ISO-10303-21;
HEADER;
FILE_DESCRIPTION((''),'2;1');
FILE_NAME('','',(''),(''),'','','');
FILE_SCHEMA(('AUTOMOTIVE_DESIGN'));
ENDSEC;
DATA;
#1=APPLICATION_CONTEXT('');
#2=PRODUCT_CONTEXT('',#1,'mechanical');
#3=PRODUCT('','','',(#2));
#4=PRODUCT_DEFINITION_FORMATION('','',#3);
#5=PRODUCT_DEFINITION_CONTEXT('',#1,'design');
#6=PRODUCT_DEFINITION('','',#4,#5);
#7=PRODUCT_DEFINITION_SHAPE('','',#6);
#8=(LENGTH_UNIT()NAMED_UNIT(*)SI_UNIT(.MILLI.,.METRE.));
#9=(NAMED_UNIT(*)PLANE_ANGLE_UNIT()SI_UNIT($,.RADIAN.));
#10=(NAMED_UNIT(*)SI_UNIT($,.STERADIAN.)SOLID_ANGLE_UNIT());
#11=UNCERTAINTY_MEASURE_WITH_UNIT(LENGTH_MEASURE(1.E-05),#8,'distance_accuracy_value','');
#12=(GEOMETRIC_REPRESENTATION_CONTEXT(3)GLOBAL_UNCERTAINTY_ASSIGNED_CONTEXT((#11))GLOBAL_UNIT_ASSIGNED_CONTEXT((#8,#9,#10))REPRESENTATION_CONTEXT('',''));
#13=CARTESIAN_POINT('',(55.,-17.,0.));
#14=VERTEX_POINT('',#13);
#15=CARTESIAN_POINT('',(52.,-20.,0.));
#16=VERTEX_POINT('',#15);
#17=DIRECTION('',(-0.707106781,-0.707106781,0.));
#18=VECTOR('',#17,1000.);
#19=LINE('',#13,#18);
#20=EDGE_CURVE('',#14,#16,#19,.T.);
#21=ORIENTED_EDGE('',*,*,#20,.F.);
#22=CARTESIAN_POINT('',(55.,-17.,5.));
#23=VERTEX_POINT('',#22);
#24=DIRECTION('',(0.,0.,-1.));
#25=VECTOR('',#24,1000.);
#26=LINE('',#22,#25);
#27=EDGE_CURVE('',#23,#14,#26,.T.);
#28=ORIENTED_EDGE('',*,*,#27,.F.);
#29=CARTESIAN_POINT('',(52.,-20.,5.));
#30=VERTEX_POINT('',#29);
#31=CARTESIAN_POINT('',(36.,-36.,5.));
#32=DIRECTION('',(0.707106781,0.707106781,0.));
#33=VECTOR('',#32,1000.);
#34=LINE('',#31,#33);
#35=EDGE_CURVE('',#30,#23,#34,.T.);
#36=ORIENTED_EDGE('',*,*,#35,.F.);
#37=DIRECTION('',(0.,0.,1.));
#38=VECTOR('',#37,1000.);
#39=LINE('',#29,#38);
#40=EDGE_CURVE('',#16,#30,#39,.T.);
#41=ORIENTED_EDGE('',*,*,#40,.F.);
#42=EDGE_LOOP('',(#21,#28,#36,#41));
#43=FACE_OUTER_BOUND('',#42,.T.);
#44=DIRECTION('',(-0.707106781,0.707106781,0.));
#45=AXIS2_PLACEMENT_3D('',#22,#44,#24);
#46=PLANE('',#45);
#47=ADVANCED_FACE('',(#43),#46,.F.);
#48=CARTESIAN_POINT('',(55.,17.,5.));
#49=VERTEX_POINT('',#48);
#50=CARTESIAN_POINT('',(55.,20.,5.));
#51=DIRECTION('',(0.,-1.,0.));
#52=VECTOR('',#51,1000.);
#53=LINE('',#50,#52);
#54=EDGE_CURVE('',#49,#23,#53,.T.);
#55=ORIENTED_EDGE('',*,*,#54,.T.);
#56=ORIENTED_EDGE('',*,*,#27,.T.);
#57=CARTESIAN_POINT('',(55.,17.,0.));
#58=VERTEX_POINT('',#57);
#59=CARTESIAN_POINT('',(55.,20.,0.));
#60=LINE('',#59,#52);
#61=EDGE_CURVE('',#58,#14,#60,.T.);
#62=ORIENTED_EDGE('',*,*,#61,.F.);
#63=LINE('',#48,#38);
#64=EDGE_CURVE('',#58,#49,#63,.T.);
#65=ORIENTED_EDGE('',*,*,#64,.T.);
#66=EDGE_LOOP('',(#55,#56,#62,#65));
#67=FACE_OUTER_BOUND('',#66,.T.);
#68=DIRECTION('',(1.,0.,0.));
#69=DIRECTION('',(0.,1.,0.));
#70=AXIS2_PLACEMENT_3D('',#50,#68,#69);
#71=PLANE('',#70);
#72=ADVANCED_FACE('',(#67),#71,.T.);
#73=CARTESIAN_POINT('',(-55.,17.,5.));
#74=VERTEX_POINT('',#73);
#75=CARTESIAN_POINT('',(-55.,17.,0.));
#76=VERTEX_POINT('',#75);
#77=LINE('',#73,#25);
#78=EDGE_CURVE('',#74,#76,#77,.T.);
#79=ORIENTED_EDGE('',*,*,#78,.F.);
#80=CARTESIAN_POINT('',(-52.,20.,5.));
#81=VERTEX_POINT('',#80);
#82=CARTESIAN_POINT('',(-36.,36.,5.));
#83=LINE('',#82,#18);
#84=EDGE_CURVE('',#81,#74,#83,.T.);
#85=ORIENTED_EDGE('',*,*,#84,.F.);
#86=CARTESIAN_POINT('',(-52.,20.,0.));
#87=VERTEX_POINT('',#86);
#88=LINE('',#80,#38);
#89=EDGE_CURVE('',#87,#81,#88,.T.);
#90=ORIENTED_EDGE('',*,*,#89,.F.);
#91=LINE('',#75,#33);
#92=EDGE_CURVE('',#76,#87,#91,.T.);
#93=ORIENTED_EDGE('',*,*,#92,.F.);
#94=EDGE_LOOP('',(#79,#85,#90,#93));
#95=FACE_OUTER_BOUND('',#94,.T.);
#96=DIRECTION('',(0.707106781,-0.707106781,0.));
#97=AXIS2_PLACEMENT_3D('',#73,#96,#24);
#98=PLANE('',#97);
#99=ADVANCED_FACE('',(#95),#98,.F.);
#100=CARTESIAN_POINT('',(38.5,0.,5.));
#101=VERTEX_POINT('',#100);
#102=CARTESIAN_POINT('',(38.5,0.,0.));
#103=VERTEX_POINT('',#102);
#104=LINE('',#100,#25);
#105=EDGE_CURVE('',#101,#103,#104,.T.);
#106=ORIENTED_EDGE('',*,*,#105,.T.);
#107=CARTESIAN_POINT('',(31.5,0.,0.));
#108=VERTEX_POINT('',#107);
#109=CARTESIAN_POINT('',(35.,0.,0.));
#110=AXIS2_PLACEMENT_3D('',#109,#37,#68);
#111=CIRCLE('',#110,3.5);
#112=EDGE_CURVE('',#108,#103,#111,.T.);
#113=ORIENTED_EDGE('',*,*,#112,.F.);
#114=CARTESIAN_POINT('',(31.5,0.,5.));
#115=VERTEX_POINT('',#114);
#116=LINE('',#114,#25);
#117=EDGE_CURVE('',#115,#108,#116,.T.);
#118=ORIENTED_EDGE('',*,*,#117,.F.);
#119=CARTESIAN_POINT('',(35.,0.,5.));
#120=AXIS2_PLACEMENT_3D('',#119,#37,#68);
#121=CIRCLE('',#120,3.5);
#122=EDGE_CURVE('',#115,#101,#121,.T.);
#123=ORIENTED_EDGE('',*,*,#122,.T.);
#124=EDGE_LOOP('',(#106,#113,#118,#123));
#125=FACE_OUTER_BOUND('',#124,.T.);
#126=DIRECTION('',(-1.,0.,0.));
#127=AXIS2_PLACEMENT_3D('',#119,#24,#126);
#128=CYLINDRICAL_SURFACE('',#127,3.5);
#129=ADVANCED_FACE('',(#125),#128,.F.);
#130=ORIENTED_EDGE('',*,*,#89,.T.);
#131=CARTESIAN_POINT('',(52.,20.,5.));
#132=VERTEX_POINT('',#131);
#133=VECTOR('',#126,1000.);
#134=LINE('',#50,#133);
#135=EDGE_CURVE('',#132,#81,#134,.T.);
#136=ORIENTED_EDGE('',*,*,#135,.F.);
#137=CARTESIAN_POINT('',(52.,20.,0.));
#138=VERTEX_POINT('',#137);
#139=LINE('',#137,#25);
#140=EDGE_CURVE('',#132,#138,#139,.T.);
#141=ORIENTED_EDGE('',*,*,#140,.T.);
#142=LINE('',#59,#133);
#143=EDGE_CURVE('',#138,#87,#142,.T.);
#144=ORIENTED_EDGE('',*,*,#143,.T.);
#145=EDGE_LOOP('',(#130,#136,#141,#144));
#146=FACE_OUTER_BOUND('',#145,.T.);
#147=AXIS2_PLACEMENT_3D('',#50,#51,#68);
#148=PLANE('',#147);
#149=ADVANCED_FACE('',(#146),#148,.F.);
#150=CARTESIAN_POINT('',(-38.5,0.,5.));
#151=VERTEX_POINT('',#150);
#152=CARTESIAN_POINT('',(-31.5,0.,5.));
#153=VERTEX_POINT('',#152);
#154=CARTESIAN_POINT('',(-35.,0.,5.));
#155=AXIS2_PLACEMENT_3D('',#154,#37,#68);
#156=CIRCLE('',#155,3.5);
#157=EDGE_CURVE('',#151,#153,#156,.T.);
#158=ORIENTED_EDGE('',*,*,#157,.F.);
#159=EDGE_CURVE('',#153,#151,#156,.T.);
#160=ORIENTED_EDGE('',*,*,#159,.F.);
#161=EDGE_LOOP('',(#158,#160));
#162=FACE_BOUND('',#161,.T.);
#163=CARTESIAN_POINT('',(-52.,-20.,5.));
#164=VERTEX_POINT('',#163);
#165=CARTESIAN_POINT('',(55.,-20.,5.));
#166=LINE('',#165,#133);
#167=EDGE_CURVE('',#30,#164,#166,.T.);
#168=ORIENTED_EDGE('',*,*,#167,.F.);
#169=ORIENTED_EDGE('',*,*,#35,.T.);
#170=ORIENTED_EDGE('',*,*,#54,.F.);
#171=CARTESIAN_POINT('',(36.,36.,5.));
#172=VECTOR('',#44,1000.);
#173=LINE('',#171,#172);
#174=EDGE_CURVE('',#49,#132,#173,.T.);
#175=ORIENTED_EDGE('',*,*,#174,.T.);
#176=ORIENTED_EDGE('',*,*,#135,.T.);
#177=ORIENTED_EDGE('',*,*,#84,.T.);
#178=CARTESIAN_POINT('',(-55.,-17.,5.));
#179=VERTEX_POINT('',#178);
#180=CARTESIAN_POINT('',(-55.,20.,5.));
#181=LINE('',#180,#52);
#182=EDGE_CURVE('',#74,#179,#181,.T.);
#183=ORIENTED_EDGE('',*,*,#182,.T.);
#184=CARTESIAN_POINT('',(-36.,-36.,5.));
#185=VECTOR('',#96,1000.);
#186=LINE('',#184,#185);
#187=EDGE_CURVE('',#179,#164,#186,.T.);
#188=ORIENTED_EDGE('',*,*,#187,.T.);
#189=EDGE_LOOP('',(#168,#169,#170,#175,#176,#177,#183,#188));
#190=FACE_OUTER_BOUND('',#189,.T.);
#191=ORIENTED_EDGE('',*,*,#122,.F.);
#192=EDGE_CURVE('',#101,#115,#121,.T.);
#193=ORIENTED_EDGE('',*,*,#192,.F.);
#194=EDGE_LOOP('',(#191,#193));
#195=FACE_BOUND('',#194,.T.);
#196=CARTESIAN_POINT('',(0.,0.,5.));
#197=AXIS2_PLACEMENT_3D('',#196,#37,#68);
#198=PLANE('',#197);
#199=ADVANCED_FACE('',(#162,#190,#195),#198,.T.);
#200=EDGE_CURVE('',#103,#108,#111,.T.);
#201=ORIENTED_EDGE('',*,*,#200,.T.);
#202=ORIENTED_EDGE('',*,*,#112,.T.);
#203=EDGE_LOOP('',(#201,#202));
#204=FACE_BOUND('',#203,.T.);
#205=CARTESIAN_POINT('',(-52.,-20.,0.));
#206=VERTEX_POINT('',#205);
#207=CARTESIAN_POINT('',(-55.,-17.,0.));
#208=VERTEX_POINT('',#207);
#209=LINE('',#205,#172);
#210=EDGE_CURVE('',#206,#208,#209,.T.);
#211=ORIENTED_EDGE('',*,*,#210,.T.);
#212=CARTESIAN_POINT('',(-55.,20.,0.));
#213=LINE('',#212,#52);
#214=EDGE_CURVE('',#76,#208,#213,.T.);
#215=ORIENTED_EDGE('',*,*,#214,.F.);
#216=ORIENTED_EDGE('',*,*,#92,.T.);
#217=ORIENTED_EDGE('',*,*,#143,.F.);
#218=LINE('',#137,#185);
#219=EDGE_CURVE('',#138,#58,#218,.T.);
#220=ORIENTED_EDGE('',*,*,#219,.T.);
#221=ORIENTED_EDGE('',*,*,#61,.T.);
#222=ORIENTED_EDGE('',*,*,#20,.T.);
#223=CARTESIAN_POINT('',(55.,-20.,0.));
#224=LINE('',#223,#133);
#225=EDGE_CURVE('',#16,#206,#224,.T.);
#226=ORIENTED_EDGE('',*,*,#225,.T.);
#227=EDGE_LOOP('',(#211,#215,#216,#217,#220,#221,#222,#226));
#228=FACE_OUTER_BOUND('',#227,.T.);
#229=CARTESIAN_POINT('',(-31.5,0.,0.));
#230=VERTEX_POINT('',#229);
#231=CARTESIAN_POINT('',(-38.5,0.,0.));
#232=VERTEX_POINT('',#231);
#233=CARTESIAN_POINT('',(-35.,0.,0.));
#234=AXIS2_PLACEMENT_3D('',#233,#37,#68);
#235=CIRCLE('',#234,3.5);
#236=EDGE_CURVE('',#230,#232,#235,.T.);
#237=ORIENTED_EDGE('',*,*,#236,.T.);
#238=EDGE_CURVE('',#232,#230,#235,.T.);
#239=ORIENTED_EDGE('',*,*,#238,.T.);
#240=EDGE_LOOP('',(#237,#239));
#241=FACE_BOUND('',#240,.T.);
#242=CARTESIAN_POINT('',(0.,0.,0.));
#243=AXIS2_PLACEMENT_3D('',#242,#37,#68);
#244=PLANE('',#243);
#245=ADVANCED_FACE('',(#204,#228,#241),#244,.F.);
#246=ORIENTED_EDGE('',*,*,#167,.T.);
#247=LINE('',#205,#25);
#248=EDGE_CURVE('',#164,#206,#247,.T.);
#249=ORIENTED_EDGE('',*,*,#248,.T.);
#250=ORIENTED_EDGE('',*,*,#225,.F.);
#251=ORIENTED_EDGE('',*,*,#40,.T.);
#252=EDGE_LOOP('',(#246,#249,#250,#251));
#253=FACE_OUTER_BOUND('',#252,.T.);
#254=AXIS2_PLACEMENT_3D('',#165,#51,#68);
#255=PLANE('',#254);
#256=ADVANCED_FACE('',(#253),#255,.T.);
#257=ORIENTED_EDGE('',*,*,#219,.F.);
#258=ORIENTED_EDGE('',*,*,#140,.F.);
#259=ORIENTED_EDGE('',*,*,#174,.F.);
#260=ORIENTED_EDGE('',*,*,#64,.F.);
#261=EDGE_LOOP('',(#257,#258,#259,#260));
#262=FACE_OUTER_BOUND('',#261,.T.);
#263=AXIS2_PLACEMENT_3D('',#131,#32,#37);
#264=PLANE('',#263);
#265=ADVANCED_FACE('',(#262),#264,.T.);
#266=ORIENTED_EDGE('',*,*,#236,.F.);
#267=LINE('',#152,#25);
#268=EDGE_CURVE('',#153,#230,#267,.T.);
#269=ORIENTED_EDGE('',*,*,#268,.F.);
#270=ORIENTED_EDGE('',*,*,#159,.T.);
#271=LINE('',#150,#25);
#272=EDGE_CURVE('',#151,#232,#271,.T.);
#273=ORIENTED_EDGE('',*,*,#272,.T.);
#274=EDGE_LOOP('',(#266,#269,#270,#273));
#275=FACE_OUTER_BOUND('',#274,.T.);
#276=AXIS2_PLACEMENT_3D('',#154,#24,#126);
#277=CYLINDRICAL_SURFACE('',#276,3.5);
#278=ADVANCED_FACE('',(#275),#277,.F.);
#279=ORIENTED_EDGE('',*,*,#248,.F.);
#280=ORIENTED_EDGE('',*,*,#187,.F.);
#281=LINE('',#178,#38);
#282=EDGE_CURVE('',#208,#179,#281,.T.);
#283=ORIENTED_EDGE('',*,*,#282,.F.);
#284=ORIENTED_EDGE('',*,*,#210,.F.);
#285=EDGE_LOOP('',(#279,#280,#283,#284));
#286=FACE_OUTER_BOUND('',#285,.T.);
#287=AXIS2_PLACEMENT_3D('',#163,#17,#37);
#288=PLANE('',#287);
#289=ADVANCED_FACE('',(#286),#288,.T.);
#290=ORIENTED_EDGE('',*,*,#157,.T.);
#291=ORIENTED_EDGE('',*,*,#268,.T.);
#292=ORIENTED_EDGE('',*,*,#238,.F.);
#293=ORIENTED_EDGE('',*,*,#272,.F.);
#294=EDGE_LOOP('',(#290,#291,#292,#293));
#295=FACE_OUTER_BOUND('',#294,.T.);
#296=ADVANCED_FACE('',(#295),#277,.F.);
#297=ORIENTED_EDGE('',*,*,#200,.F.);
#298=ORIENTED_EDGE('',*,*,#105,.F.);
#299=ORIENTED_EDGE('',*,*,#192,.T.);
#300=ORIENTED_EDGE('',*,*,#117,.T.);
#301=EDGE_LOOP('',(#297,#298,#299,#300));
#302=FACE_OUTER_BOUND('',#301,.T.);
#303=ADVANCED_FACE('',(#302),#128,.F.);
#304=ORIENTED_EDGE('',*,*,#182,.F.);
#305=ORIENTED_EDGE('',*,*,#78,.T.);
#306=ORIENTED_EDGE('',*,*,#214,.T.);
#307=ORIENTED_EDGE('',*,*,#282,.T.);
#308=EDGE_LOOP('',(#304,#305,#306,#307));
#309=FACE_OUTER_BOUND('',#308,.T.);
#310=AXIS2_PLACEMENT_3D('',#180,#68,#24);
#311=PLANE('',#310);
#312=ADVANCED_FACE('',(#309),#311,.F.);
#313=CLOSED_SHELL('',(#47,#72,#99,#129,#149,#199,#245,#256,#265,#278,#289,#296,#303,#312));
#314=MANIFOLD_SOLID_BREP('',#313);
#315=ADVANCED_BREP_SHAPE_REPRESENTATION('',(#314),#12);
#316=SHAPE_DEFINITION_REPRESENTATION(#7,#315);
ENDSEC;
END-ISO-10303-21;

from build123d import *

# Parameters (mm, degrees)
SKETCH1_W           = 110
SKETCH1_H           = 40
SKETCH1_R           = 3.5
BOSS_EXTRUDE1_DEPTH = 5
CHAMFER1_SIZE       = 3


with BuildPart() as part:
    # Sketch1 → Boss-Extrude1 (new body)
    with BuildSketch(Plane.XY):
        Rectangle(SKETCH1_W, SKETCH1_H)
        with Locations((-35, 0)):
            Circle(SKETCH1_R, mode=Mode.SUBTRACT)
        with Locations((35, 0)):
            Circle(SKETCH1_R, mode=Mode.SUBTRACT)
    extrude(amount=BOSS_EXTRUDE1_DEPTH)

    # Chamfer1
    chamfer1_edges = [part.edges().sort_by_distance(p)[0] for p in [
        (55, -20, 2.5),
        (55, 20, 2.5),
        (-55, 20, 2.5),
        (-55, -20, 2.5),
    ]]
    chamfer(chamfer1_edges, length=CHAMFER1_SIZE)


solid = part.part
